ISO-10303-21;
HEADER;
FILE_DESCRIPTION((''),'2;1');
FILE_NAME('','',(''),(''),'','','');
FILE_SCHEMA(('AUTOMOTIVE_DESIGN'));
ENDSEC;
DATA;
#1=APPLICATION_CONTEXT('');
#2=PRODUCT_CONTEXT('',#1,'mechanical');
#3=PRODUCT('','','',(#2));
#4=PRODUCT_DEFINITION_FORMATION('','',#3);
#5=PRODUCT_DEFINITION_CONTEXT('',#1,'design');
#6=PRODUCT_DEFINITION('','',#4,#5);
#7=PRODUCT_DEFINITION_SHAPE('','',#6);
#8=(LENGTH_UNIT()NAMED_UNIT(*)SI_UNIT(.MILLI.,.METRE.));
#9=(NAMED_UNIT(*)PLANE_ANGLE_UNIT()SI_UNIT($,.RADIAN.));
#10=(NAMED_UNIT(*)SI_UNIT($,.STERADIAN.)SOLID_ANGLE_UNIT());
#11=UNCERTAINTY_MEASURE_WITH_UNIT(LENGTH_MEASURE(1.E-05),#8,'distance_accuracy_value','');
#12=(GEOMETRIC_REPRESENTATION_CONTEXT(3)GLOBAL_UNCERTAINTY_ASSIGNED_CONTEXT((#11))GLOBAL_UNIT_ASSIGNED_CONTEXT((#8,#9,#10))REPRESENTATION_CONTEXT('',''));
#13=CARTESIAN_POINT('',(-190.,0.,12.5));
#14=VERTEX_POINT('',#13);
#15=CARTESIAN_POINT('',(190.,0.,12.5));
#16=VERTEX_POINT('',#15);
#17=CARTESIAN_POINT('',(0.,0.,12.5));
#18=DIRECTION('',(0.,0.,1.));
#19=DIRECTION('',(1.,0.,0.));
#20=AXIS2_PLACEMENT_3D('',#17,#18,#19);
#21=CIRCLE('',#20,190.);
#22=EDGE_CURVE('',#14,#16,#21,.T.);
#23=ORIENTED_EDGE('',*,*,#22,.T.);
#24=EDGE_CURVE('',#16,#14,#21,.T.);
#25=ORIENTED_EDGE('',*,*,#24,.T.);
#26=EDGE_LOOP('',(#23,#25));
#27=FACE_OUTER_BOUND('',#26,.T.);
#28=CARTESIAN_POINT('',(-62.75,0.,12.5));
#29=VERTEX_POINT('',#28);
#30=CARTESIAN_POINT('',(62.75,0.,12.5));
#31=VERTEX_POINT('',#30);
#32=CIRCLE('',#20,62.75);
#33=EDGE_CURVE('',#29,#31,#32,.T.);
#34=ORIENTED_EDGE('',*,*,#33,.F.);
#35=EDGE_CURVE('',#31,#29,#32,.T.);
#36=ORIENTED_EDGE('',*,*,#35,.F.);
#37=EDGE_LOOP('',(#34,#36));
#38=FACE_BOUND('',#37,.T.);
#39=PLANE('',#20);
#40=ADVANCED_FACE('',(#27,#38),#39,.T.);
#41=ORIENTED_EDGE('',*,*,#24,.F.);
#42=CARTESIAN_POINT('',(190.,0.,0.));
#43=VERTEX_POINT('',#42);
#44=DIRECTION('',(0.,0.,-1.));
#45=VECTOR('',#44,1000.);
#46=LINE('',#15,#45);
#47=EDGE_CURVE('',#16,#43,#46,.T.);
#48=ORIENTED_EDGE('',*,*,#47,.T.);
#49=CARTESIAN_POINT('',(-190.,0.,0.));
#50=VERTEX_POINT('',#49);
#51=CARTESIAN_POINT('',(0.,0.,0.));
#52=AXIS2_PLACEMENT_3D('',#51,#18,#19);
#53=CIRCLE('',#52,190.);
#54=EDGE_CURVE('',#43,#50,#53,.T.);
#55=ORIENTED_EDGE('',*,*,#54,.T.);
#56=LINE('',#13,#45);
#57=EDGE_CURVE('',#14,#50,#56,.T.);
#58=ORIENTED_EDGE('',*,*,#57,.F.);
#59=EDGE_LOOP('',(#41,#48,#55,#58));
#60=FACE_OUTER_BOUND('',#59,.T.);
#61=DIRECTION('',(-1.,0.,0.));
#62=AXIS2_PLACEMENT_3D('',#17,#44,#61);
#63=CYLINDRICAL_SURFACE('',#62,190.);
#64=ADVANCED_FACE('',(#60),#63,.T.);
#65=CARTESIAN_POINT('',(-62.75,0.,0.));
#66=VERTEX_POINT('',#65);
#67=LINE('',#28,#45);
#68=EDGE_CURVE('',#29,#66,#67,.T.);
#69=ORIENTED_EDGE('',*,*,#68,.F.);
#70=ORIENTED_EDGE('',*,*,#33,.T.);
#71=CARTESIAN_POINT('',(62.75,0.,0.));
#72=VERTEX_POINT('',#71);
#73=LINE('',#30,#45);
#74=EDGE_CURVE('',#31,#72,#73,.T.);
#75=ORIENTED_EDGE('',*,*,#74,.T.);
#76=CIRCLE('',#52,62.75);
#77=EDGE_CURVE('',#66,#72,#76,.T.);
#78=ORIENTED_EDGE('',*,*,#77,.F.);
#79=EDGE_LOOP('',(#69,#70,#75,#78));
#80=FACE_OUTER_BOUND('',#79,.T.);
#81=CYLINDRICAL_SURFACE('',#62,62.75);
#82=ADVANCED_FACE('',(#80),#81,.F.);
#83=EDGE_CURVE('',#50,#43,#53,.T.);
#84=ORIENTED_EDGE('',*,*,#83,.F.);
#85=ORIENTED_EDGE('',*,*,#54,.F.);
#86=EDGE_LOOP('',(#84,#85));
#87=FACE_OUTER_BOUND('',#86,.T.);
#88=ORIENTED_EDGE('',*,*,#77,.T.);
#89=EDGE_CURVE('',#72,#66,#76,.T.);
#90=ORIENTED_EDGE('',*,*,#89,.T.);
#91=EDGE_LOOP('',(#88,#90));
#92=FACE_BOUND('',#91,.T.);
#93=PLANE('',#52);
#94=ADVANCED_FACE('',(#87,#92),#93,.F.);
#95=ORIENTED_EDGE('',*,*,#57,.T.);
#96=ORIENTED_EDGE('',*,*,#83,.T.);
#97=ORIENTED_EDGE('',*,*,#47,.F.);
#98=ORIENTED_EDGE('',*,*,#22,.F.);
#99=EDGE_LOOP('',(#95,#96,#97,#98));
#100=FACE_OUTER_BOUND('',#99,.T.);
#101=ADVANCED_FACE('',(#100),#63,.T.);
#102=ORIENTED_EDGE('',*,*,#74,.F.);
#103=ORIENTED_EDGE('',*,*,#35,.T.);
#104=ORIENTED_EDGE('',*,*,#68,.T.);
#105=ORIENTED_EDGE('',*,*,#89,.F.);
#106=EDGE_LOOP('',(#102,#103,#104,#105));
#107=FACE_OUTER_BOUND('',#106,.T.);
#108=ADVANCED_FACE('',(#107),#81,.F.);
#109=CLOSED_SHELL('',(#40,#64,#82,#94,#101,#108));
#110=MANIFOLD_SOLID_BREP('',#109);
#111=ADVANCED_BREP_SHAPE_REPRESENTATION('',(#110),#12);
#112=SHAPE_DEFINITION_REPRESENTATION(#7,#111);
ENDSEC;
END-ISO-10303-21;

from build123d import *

# Parameters (mm, degrees)
SKETCH1_R           = 190
SKETCH1_R_2         = 62.75
BOSS_EXTRUDE1_DEPTH = 12.5


with BuildPart() as part:
    # Sketch1 → Boss-Extrude1 (new body)
    with BuildSketch(Plane.XY):
        Circle(SKETCH1_R)
        Circle(SKETCH1_R_2, mode=Mode.SUBTRACT)
    extrude(amount=BOSS_EXTRUDE1_DEPTH)


solid = part.part
